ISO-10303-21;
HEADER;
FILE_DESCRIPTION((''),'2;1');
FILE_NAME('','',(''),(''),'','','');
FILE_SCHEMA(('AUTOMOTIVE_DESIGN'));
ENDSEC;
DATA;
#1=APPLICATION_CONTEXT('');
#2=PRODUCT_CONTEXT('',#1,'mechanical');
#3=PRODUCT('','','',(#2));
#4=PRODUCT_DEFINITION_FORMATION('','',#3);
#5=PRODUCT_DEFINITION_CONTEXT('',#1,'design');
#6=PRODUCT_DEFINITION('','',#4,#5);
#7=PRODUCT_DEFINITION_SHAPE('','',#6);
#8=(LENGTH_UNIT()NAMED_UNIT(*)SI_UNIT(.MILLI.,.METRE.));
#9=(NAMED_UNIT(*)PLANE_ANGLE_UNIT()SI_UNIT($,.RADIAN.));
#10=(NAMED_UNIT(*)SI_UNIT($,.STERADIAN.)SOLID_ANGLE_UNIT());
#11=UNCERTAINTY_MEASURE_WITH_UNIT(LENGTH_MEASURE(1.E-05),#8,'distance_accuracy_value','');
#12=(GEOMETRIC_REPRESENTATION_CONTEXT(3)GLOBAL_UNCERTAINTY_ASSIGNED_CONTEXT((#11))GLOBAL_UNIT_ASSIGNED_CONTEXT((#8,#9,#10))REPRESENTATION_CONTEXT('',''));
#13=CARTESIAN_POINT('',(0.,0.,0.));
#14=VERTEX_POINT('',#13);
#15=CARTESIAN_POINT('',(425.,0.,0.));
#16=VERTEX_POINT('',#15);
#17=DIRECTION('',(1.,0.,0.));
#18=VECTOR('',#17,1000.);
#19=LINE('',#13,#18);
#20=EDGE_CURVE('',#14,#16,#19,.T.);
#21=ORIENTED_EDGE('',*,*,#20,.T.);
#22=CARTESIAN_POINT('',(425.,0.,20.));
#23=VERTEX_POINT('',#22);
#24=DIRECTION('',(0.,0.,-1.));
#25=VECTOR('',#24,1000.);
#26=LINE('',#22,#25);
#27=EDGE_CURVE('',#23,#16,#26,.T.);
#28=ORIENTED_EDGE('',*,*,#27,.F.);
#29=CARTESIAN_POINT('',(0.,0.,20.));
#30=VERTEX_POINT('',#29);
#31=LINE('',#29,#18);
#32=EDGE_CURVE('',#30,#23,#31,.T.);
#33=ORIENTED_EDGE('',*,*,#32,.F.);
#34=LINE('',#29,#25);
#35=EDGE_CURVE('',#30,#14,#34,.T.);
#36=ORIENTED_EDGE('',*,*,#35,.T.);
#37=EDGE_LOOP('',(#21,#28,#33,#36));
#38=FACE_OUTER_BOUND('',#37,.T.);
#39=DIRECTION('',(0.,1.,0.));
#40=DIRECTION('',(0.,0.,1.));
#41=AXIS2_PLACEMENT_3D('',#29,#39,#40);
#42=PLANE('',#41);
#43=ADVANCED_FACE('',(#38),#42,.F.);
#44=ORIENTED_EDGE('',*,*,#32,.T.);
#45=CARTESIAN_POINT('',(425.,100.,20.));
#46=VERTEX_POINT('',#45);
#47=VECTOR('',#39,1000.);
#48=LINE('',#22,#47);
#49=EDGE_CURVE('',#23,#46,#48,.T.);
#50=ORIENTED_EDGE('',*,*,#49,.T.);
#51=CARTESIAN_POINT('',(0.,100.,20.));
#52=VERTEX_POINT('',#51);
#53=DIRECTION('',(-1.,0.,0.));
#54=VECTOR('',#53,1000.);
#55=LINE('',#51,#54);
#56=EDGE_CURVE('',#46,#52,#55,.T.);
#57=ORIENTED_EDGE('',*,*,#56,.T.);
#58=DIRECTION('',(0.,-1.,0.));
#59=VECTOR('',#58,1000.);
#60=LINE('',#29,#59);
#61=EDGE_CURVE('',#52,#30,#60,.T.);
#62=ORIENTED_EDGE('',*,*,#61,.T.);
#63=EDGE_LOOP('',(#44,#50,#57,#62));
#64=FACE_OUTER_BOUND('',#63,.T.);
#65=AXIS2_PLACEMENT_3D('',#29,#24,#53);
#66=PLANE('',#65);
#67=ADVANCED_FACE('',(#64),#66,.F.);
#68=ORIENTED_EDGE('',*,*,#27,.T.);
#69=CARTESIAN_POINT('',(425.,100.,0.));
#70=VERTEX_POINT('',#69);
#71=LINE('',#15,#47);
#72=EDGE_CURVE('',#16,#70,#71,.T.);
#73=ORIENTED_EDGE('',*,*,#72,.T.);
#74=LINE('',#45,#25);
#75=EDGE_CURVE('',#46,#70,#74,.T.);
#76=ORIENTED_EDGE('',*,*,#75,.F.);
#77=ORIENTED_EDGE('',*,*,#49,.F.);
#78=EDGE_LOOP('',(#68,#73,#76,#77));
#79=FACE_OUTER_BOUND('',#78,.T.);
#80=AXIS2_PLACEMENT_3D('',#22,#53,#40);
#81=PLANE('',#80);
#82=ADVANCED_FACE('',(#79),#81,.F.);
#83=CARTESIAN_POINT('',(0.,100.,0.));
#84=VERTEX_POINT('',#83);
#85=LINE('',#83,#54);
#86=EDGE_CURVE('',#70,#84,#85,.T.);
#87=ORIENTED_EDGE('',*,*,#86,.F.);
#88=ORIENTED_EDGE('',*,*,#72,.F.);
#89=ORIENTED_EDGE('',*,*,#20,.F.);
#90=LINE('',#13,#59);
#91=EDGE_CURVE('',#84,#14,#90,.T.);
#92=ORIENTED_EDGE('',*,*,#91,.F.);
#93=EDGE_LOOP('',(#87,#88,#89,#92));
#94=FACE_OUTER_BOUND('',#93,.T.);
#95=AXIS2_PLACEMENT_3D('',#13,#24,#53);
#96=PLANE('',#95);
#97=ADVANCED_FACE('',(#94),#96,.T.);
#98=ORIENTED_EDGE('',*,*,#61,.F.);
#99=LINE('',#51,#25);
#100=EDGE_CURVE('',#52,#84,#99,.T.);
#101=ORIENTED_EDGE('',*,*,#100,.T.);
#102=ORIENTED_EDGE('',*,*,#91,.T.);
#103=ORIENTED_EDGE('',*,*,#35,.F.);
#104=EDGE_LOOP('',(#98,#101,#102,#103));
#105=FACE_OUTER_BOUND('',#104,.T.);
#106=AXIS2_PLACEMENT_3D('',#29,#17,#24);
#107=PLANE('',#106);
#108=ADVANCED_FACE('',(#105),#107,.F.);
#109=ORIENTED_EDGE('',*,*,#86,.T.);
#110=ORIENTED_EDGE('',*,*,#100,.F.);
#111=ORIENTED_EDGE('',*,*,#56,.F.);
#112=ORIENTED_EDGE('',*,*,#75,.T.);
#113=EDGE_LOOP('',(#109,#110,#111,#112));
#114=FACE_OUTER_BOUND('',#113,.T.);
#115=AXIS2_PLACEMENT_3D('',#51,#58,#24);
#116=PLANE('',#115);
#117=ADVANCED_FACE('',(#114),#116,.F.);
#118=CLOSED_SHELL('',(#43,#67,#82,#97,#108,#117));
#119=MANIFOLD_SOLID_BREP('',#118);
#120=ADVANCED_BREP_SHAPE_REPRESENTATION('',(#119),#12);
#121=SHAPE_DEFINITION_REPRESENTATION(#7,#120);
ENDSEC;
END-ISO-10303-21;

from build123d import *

# Parameters (mm, degrees)
SKETCH1_W           = 425
SKETCH1_H           = 100
BOSS_EXTRUDE1_DEPTH = 20


with BuildPart() as part:
    # Sketch1 → Boss-Extrude1 (new body)
    with BuildSketch(Plane.XY):
        with Locations((212.5, 50)):
            Rectangle(SKETCH1_W, SKETCH1_H)
    extrude(amount=BOSS_EXTRUDE1_DEPTH)


solid = part.part
